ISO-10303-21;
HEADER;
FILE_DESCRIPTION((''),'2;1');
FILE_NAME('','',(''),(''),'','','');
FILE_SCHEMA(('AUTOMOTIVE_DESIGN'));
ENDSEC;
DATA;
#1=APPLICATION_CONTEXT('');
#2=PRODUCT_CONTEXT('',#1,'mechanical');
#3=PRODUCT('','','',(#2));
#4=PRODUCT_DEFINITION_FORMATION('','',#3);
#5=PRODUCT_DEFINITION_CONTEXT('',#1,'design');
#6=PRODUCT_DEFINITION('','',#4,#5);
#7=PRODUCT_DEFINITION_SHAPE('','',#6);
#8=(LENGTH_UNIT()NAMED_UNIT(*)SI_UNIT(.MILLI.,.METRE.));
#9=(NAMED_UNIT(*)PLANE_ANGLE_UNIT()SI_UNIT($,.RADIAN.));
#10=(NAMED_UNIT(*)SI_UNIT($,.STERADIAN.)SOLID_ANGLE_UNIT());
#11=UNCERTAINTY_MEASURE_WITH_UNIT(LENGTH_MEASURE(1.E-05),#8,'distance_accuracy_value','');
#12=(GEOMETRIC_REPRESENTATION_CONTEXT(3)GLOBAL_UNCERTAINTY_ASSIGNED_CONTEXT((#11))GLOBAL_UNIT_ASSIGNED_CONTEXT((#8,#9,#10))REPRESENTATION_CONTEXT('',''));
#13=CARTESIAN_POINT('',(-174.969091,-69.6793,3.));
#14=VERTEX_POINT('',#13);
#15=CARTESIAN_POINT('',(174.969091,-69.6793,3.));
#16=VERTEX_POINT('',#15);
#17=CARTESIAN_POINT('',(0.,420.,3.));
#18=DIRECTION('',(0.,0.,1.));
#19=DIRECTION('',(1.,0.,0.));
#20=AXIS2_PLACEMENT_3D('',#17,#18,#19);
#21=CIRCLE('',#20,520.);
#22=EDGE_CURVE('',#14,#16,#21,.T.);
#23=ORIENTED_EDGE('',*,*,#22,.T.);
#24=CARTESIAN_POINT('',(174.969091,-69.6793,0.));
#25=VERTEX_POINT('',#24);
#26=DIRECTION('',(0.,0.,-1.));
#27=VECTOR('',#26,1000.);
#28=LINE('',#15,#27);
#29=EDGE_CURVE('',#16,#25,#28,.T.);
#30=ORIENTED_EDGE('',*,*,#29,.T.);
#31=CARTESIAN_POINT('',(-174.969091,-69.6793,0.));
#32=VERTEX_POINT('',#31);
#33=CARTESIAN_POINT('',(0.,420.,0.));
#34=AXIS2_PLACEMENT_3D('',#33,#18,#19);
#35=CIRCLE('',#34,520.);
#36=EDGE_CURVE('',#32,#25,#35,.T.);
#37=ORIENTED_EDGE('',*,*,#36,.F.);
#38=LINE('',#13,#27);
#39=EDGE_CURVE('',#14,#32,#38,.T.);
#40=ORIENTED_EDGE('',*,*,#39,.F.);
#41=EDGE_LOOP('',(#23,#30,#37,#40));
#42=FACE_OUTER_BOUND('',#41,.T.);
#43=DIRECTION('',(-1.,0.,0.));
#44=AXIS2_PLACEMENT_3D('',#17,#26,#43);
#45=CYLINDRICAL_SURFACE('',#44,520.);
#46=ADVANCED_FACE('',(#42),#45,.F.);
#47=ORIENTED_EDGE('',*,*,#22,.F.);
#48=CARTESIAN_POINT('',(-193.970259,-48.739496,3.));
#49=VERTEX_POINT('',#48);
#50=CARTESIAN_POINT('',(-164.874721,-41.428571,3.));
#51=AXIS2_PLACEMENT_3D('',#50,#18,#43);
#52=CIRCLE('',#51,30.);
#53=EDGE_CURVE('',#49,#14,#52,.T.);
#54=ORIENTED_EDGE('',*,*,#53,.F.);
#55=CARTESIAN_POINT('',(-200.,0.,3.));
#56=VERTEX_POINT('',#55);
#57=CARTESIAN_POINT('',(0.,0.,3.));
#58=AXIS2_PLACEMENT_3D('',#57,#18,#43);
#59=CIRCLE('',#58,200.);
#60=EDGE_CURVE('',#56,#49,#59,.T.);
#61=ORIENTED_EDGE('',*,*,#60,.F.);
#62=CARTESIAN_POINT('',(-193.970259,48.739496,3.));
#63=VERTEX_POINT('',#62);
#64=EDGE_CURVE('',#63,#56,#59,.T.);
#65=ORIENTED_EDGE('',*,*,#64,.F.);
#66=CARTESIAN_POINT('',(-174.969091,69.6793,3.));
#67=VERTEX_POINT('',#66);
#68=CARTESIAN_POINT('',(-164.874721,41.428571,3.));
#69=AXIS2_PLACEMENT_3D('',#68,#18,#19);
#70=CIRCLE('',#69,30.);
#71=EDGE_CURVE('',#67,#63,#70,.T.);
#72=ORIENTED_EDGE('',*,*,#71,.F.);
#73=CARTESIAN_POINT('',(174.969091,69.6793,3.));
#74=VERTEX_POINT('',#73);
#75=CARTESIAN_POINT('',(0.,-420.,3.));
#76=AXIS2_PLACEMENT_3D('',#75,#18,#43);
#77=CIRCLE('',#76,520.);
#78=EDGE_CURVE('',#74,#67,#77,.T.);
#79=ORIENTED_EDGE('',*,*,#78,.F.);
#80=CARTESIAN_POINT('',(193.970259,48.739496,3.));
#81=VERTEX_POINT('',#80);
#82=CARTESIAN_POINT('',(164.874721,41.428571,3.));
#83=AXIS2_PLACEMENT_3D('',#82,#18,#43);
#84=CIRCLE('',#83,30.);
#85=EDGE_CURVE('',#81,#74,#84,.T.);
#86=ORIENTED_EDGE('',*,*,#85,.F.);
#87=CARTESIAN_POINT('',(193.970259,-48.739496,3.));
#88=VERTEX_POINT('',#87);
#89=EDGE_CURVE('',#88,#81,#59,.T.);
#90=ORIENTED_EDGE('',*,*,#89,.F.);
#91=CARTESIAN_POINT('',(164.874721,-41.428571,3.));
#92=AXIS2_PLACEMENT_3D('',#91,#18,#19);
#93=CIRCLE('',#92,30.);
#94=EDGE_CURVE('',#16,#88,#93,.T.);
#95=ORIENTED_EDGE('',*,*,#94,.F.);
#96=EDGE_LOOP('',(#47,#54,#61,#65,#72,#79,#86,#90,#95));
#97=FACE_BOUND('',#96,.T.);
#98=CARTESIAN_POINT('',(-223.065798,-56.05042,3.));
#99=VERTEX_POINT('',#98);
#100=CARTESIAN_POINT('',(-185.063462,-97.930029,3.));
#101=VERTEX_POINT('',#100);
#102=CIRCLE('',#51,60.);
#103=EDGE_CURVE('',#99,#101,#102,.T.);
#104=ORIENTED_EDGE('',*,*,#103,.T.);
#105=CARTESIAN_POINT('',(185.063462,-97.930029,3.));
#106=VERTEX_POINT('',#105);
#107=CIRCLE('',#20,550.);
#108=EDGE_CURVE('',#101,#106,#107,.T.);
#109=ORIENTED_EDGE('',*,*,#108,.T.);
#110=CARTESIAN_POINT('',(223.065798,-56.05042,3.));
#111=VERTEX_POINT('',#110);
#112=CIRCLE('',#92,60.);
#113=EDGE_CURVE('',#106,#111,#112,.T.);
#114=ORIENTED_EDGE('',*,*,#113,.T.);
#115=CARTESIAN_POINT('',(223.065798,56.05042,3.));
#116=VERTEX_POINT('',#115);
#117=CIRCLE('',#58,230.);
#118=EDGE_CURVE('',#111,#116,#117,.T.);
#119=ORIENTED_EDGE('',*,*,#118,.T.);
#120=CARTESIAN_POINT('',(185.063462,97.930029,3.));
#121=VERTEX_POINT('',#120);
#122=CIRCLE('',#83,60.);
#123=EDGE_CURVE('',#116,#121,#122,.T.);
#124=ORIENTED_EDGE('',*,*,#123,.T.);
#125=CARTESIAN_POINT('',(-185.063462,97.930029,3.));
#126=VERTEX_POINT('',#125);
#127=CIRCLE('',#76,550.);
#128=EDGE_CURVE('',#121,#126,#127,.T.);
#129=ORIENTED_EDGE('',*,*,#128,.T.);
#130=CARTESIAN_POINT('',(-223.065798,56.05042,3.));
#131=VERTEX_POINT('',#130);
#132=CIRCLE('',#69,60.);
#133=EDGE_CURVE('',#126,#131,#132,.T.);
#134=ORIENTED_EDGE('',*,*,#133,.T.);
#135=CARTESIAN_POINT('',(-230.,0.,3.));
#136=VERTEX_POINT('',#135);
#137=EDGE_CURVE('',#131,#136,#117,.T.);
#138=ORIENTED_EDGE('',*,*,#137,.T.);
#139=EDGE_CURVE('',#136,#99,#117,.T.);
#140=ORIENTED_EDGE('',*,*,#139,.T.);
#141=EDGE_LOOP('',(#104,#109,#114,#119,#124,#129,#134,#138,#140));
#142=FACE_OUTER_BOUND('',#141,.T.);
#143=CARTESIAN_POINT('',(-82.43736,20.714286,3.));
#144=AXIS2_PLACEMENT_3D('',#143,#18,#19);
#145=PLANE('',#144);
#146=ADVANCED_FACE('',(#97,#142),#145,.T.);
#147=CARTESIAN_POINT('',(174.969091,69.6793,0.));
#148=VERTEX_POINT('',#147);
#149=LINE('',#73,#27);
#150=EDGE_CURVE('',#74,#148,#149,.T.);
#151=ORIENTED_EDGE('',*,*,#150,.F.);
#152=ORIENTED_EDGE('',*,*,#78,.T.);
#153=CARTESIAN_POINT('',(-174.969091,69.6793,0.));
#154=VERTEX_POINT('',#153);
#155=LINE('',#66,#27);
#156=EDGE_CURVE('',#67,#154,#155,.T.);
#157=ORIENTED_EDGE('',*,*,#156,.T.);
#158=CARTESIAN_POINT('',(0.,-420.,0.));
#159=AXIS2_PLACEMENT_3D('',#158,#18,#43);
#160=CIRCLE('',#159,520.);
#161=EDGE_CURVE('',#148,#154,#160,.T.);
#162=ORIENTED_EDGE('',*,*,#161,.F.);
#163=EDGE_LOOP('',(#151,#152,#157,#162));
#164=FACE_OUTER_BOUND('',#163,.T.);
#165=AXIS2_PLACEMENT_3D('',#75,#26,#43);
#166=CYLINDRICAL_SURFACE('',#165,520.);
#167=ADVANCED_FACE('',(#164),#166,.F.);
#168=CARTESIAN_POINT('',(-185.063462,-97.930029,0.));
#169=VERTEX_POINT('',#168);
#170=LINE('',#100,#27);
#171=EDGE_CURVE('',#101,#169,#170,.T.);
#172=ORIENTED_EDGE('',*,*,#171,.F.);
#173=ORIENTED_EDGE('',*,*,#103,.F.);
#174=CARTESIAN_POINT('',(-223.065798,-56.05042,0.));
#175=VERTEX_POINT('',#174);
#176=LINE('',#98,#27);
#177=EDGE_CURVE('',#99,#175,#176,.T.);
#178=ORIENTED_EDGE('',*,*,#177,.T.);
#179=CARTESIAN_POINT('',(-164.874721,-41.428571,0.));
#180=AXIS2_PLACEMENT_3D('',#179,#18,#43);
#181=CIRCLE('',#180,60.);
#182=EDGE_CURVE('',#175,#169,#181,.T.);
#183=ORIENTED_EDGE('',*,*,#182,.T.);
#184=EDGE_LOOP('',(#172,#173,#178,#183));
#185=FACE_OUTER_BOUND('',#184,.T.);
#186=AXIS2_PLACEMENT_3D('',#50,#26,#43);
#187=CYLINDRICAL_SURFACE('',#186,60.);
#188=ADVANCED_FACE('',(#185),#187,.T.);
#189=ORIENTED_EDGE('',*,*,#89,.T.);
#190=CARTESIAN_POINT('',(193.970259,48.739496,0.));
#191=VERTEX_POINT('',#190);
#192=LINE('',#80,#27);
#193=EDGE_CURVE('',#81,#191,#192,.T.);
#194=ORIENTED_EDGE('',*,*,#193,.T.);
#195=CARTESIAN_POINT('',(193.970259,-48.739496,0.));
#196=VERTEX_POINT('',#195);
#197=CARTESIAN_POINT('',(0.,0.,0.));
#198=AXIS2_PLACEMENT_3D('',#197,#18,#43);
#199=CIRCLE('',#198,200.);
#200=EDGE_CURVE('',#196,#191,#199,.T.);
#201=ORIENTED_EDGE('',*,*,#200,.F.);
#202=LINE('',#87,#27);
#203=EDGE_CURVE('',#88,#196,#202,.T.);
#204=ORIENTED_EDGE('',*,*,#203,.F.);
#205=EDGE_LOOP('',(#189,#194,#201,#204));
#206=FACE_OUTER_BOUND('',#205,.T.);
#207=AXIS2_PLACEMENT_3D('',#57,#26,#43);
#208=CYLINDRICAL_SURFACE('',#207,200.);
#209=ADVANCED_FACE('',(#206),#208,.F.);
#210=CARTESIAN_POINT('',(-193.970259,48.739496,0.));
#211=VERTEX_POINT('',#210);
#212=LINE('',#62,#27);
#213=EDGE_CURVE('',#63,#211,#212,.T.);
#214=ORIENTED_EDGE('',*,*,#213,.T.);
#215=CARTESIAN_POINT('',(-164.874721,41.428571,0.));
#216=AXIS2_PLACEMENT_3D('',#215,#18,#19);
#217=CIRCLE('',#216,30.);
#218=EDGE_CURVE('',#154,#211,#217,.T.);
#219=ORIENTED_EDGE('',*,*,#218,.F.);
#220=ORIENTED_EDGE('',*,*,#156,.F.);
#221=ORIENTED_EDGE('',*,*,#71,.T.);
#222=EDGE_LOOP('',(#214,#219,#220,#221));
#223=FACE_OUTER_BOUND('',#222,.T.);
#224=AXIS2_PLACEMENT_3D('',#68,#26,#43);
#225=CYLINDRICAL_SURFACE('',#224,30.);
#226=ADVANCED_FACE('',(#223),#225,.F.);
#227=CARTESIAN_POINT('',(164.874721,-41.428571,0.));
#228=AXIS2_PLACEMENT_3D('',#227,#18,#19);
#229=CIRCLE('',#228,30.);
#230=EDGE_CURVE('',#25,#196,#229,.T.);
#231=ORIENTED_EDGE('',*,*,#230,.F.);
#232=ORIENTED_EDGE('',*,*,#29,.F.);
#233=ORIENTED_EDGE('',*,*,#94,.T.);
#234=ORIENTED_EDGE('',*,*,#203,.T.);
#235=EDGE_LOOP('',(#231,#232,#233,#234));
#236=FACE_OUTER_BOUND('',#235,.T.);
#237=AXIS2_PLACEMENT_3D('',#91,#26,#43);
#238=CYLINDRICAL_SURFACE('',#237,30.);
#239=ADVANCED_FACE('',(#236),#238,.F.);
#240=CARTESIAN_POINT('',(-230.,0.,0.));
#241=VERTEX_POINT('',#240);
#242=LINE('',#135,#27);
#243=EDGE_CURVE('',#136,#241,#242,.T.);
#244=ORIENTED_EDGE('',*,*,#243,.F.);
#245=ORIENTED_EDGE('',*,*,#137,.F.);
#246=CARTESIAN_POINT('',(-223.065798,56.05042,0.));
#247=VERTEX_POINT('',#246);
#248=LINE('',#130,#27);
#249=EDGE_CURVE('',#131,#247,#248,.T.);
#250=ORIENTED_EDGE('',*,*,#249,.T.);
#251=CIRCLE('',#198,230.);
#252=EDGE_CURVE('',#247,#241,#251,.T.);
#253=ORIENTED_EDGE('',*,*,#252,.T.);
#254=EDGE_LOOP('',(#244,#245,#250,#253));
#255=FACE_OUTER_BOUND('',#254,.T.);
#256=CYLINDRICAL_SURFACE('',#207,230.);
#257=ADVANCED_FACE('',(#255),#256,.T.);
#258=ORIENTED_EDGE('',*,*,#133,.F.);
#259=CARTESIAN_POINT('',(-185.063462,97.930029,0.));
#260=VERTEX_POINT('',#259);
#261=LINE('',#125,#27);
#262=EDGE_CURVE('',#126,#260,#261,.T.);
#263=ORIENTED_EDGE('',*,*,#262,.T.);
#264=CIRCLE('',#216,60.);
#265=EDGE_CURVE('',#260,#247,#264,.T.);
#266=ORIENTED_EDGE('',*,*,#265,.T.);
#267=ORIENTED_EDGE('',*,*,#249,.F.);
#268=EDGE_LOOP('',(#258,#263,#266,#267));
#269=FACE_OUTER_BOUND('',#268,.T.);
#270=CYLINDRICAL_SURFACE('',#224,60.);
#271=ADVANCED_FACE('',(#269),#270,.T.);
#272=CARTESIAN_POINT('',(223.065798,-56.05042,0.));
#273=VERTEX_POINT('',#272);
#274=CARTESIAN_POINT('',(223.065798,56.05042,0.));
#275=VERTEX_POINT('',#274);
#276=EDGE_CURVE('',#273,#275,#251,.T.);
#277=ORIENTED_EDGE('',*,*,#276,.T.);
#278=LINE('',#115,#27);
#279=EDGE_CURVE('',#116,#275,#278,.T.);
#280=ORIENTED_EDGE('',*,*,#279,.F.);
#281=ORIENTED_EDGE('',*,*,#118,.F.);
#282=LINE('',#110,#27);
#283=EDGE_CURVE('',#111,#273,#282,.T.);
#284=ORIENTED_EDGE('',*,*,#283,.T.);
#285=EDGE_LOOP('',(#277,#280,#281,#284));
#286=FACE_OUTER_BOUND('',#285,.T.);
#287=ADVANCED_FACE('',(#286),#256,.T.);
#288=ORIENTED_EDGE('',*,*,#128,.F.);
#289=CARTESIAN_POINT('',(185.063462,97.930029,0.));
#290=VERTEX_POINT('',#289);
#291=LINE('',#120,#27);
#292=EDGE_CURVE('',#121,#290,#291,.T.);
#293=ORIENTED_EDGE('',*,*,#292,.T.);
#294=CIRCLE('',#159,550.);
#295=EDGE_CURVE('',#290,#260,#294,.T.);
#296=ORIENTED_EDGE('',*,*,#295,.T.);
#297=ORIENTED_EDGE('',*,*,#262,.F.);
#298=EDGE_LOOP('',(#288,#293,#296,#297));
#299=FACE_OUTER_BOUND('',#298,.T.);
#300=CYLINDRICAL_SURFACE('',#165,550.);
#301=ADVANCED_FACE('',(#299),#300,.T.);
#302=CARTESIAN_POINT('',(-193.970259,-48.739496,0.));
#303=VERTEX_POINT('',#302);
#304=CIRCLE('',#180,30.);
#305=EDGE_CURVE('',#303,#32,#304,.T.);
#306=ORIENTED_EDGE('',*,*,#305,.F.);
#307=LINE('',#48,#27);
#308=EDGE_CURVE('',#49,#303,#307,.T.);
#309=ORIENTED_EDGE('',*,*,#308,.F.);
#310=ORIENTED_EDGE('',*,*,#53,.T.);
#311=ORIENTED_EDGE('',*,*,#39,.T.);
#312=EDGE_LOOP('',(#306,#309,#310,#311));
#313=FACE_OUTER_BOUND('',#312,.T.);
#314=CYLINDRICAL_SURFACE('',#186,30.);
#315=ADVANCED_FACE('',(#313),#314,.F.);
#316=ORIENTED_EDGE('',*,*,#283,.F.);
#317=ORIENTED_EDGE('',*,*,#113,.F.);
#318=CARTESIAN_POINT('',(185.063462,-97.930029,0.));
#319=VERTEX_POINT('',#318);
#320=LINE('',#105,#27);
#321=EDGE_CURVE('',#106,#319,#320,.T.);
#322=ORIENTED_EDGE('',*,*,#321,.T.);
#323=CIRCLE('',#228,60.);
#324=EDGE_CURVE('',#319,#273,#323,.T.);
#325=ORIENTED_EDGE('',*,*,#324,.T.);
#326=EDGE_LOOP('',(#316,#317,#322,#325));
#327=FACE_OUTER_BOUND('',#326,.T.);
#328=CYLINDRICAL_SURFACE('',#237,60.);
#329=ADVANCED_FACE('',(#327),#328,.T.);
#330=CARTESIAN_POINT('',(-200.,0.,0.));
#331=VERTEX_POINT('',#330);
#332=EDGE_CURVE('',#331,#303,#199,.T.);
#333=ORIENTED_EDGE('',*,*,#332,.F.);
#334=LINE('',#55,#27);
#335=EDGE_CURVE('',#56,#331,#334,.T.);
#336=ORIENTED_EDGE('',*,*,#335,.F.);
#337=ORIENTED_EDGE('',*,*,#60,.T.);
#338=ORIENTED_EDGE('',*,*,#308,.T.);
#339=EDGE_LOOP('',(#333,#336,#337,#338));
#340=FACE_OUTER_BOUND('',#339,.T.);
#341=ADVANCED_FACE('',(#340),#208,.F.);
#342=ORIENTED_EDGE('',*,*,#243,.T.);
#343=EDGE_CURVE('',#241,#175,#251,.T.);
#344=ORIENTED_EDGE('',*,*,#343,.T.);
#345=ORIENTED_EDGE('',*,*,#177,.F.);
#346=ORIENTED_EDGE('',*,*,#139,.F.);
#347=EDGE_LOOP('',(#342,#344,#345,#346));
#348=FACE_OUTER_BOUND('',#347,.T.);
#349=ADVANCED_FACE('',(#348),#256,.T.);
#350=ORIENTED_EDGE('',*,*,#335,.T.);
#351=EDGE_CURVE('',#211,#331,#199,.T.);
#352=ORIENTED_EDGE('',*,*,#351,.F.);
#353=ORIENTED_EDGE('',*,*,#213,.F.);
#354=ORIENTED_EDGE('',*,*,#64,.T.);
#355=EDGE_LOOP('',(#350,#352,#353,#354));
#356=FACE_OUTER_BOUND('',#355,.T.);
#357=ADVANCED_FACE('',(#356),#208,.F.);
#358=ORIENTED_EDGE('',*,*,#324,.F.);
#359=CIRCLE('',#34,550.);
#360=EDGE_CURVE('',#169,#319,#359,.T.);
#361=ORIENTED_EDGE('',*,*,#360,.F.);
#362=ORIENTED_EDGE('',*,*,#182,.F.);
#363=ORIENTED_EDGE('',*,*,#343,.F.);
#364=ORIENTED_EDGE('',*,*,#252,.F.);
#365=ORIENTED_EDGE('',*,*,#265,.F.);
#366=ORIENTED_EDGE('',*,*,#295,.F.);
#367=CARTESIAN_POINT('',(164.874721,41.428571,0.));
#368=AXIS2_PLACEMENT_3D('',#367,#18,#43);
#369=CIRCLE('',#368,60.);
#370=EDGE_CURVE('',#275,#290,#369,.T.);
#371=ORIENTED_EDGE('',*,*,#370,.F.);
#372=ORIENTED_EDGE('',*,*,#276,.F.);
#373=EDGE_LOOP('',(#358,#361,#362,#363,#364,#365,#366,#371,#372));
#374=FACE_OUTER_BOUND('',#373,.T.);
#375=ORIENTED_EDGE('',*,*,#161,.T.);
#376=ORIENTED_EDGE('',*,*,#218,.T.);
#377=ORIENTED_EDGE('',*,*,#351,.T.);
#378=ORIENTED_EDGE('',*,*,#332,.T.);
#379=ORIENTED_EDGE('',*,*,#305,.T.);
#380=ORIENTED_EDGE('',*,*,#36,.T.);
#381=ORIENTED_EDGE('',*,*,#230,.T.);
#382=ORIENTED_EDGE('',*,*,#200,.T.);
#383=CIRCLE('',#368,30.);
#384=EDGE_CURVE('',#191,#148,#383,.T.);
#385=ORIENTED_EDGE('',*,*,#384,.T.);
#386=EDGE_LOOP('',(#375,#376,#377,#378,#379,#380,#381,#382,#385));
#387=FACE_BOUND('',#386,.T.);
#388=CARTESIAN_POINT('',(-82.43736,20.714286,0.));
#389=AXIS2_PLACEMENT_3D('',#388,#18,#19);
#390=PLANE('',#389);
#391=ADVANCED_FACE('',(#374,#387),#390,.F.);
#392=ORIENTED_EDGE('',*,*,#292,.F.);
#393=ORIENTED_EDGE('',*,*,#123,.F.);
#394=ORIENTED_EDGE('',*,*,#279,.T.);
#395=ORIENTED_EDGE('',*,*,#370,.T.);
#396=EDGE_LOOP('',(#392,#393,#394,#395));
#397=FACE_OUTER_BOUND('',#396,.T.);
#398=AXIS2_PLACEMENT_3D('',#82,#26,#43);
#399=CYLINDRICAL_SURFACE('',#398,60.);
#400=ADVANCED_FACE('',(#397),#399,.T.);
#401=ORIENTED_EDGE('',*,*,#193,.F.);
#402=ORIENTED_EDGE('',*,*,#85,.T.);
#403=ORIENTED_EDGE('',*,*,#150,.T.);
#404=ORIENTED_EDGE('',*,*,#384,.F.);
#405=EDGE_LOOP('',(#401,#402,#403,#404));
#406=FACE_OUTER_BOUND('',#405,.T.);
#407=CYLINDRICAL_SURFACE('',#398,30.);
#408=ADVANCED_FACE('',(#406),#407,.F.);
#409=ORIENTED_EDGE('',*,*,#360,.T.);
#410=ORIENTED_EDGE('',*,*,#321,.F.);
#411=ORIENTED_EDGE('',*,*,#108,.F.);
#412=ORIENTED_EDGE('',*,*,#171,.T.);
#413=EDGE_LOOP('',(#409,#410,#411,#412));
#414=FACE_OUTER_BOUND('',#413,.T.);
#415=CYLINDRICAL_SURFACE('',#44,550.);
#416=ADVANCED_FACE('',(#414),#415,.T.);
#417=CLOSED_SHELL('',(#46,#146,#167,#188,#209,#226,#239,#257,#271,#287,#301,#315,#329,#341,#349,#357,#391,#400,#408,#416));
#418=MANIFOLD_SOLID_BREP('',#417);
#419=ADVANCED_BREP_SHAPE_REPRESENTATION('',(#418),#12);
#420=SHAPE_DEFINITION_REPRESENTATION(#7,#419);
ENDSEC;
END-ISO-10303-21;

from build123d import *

# Parameters (mm, degrees)
BOSS_EXTRUDE1_DEPTH = 3


with BuildPart() as part:
    # Sketch1 → Boss-Extrude1 (new body)
    with BuildSketch(Plane.XY):
        with BuildLine():
            ThreePointArc((-185.063461818, 97.930029155), (0, 130), (185.063461818, 97.930029155))
            ThreePointArc((185.063461818, 97.930029155), (209.308091137, 81.748238793), (223.065798362, 56.050420168))
            ThreePointArc((223.065798362, 56.050420168), (230, 0), (223.065798362, -56.050420168))
            ThreePointArc((223.065798362, -56.050420168), (209.308091137, -81.748238793), (185.063461818, -97.930029155))
            ThreePointArc((185.063461818, -97.930029155), (0, -130), (-185.063461818, -97.930029155))
            ThreePointArc((-185.063461818, -97.930029155), (-209.308091137, -81.748238793), (-223.065798362, -56.050420168))
            ThreePointArc((-223.065798362, -56.050420168), (-230, 0), (-223.065798362, 56.050420168))
            ThreePointArc((-223.065798362, 56.050420168), (-209.308091137, 81.748238793), (-185.063461818, 97.930029155))
        make_face()
        with BuildLine():
            ThreePointArc((-174.969091173, 69.679300292), (0, 100), (174.969091173, 69.679300292))
            ThreePointArc((174.969091173, 69.679300292), (187.091405833, 61.588405111), (193.970259445, 48.739495798))
            ThreePointArc((193.970259445, 48.739495798), (200, 0), (193.970259445, -48.739495798))
            ThreePointArc((193.970259445, -48.739495798), (187.091405833, -61.588405111), (174.969091173, -69.679300292))
            ThreePointArc((174.969091173, -69.679300292), (0, -100), (-174.969091173, -69.679300292))
            ThreePointArc((-174.969091173, -69.679300292), (-187.091405833, -61.588405111), (-193.970259445, -48.739495798))
            ThreePointArc((-193.970259445, -48.739495798), (-200, 0), (-193.970259445, 48.739495798))
            ThreePointArc((-193.970259445, 48.739495798), (-187.091405833, 61.588405111), (-174.969091173, 69.679300292))
        make_face(mode=Mode.SUBTRACT)
    extrude(amount=BOSS_EXTRUDE1_DEPTH)


solid = part.part
